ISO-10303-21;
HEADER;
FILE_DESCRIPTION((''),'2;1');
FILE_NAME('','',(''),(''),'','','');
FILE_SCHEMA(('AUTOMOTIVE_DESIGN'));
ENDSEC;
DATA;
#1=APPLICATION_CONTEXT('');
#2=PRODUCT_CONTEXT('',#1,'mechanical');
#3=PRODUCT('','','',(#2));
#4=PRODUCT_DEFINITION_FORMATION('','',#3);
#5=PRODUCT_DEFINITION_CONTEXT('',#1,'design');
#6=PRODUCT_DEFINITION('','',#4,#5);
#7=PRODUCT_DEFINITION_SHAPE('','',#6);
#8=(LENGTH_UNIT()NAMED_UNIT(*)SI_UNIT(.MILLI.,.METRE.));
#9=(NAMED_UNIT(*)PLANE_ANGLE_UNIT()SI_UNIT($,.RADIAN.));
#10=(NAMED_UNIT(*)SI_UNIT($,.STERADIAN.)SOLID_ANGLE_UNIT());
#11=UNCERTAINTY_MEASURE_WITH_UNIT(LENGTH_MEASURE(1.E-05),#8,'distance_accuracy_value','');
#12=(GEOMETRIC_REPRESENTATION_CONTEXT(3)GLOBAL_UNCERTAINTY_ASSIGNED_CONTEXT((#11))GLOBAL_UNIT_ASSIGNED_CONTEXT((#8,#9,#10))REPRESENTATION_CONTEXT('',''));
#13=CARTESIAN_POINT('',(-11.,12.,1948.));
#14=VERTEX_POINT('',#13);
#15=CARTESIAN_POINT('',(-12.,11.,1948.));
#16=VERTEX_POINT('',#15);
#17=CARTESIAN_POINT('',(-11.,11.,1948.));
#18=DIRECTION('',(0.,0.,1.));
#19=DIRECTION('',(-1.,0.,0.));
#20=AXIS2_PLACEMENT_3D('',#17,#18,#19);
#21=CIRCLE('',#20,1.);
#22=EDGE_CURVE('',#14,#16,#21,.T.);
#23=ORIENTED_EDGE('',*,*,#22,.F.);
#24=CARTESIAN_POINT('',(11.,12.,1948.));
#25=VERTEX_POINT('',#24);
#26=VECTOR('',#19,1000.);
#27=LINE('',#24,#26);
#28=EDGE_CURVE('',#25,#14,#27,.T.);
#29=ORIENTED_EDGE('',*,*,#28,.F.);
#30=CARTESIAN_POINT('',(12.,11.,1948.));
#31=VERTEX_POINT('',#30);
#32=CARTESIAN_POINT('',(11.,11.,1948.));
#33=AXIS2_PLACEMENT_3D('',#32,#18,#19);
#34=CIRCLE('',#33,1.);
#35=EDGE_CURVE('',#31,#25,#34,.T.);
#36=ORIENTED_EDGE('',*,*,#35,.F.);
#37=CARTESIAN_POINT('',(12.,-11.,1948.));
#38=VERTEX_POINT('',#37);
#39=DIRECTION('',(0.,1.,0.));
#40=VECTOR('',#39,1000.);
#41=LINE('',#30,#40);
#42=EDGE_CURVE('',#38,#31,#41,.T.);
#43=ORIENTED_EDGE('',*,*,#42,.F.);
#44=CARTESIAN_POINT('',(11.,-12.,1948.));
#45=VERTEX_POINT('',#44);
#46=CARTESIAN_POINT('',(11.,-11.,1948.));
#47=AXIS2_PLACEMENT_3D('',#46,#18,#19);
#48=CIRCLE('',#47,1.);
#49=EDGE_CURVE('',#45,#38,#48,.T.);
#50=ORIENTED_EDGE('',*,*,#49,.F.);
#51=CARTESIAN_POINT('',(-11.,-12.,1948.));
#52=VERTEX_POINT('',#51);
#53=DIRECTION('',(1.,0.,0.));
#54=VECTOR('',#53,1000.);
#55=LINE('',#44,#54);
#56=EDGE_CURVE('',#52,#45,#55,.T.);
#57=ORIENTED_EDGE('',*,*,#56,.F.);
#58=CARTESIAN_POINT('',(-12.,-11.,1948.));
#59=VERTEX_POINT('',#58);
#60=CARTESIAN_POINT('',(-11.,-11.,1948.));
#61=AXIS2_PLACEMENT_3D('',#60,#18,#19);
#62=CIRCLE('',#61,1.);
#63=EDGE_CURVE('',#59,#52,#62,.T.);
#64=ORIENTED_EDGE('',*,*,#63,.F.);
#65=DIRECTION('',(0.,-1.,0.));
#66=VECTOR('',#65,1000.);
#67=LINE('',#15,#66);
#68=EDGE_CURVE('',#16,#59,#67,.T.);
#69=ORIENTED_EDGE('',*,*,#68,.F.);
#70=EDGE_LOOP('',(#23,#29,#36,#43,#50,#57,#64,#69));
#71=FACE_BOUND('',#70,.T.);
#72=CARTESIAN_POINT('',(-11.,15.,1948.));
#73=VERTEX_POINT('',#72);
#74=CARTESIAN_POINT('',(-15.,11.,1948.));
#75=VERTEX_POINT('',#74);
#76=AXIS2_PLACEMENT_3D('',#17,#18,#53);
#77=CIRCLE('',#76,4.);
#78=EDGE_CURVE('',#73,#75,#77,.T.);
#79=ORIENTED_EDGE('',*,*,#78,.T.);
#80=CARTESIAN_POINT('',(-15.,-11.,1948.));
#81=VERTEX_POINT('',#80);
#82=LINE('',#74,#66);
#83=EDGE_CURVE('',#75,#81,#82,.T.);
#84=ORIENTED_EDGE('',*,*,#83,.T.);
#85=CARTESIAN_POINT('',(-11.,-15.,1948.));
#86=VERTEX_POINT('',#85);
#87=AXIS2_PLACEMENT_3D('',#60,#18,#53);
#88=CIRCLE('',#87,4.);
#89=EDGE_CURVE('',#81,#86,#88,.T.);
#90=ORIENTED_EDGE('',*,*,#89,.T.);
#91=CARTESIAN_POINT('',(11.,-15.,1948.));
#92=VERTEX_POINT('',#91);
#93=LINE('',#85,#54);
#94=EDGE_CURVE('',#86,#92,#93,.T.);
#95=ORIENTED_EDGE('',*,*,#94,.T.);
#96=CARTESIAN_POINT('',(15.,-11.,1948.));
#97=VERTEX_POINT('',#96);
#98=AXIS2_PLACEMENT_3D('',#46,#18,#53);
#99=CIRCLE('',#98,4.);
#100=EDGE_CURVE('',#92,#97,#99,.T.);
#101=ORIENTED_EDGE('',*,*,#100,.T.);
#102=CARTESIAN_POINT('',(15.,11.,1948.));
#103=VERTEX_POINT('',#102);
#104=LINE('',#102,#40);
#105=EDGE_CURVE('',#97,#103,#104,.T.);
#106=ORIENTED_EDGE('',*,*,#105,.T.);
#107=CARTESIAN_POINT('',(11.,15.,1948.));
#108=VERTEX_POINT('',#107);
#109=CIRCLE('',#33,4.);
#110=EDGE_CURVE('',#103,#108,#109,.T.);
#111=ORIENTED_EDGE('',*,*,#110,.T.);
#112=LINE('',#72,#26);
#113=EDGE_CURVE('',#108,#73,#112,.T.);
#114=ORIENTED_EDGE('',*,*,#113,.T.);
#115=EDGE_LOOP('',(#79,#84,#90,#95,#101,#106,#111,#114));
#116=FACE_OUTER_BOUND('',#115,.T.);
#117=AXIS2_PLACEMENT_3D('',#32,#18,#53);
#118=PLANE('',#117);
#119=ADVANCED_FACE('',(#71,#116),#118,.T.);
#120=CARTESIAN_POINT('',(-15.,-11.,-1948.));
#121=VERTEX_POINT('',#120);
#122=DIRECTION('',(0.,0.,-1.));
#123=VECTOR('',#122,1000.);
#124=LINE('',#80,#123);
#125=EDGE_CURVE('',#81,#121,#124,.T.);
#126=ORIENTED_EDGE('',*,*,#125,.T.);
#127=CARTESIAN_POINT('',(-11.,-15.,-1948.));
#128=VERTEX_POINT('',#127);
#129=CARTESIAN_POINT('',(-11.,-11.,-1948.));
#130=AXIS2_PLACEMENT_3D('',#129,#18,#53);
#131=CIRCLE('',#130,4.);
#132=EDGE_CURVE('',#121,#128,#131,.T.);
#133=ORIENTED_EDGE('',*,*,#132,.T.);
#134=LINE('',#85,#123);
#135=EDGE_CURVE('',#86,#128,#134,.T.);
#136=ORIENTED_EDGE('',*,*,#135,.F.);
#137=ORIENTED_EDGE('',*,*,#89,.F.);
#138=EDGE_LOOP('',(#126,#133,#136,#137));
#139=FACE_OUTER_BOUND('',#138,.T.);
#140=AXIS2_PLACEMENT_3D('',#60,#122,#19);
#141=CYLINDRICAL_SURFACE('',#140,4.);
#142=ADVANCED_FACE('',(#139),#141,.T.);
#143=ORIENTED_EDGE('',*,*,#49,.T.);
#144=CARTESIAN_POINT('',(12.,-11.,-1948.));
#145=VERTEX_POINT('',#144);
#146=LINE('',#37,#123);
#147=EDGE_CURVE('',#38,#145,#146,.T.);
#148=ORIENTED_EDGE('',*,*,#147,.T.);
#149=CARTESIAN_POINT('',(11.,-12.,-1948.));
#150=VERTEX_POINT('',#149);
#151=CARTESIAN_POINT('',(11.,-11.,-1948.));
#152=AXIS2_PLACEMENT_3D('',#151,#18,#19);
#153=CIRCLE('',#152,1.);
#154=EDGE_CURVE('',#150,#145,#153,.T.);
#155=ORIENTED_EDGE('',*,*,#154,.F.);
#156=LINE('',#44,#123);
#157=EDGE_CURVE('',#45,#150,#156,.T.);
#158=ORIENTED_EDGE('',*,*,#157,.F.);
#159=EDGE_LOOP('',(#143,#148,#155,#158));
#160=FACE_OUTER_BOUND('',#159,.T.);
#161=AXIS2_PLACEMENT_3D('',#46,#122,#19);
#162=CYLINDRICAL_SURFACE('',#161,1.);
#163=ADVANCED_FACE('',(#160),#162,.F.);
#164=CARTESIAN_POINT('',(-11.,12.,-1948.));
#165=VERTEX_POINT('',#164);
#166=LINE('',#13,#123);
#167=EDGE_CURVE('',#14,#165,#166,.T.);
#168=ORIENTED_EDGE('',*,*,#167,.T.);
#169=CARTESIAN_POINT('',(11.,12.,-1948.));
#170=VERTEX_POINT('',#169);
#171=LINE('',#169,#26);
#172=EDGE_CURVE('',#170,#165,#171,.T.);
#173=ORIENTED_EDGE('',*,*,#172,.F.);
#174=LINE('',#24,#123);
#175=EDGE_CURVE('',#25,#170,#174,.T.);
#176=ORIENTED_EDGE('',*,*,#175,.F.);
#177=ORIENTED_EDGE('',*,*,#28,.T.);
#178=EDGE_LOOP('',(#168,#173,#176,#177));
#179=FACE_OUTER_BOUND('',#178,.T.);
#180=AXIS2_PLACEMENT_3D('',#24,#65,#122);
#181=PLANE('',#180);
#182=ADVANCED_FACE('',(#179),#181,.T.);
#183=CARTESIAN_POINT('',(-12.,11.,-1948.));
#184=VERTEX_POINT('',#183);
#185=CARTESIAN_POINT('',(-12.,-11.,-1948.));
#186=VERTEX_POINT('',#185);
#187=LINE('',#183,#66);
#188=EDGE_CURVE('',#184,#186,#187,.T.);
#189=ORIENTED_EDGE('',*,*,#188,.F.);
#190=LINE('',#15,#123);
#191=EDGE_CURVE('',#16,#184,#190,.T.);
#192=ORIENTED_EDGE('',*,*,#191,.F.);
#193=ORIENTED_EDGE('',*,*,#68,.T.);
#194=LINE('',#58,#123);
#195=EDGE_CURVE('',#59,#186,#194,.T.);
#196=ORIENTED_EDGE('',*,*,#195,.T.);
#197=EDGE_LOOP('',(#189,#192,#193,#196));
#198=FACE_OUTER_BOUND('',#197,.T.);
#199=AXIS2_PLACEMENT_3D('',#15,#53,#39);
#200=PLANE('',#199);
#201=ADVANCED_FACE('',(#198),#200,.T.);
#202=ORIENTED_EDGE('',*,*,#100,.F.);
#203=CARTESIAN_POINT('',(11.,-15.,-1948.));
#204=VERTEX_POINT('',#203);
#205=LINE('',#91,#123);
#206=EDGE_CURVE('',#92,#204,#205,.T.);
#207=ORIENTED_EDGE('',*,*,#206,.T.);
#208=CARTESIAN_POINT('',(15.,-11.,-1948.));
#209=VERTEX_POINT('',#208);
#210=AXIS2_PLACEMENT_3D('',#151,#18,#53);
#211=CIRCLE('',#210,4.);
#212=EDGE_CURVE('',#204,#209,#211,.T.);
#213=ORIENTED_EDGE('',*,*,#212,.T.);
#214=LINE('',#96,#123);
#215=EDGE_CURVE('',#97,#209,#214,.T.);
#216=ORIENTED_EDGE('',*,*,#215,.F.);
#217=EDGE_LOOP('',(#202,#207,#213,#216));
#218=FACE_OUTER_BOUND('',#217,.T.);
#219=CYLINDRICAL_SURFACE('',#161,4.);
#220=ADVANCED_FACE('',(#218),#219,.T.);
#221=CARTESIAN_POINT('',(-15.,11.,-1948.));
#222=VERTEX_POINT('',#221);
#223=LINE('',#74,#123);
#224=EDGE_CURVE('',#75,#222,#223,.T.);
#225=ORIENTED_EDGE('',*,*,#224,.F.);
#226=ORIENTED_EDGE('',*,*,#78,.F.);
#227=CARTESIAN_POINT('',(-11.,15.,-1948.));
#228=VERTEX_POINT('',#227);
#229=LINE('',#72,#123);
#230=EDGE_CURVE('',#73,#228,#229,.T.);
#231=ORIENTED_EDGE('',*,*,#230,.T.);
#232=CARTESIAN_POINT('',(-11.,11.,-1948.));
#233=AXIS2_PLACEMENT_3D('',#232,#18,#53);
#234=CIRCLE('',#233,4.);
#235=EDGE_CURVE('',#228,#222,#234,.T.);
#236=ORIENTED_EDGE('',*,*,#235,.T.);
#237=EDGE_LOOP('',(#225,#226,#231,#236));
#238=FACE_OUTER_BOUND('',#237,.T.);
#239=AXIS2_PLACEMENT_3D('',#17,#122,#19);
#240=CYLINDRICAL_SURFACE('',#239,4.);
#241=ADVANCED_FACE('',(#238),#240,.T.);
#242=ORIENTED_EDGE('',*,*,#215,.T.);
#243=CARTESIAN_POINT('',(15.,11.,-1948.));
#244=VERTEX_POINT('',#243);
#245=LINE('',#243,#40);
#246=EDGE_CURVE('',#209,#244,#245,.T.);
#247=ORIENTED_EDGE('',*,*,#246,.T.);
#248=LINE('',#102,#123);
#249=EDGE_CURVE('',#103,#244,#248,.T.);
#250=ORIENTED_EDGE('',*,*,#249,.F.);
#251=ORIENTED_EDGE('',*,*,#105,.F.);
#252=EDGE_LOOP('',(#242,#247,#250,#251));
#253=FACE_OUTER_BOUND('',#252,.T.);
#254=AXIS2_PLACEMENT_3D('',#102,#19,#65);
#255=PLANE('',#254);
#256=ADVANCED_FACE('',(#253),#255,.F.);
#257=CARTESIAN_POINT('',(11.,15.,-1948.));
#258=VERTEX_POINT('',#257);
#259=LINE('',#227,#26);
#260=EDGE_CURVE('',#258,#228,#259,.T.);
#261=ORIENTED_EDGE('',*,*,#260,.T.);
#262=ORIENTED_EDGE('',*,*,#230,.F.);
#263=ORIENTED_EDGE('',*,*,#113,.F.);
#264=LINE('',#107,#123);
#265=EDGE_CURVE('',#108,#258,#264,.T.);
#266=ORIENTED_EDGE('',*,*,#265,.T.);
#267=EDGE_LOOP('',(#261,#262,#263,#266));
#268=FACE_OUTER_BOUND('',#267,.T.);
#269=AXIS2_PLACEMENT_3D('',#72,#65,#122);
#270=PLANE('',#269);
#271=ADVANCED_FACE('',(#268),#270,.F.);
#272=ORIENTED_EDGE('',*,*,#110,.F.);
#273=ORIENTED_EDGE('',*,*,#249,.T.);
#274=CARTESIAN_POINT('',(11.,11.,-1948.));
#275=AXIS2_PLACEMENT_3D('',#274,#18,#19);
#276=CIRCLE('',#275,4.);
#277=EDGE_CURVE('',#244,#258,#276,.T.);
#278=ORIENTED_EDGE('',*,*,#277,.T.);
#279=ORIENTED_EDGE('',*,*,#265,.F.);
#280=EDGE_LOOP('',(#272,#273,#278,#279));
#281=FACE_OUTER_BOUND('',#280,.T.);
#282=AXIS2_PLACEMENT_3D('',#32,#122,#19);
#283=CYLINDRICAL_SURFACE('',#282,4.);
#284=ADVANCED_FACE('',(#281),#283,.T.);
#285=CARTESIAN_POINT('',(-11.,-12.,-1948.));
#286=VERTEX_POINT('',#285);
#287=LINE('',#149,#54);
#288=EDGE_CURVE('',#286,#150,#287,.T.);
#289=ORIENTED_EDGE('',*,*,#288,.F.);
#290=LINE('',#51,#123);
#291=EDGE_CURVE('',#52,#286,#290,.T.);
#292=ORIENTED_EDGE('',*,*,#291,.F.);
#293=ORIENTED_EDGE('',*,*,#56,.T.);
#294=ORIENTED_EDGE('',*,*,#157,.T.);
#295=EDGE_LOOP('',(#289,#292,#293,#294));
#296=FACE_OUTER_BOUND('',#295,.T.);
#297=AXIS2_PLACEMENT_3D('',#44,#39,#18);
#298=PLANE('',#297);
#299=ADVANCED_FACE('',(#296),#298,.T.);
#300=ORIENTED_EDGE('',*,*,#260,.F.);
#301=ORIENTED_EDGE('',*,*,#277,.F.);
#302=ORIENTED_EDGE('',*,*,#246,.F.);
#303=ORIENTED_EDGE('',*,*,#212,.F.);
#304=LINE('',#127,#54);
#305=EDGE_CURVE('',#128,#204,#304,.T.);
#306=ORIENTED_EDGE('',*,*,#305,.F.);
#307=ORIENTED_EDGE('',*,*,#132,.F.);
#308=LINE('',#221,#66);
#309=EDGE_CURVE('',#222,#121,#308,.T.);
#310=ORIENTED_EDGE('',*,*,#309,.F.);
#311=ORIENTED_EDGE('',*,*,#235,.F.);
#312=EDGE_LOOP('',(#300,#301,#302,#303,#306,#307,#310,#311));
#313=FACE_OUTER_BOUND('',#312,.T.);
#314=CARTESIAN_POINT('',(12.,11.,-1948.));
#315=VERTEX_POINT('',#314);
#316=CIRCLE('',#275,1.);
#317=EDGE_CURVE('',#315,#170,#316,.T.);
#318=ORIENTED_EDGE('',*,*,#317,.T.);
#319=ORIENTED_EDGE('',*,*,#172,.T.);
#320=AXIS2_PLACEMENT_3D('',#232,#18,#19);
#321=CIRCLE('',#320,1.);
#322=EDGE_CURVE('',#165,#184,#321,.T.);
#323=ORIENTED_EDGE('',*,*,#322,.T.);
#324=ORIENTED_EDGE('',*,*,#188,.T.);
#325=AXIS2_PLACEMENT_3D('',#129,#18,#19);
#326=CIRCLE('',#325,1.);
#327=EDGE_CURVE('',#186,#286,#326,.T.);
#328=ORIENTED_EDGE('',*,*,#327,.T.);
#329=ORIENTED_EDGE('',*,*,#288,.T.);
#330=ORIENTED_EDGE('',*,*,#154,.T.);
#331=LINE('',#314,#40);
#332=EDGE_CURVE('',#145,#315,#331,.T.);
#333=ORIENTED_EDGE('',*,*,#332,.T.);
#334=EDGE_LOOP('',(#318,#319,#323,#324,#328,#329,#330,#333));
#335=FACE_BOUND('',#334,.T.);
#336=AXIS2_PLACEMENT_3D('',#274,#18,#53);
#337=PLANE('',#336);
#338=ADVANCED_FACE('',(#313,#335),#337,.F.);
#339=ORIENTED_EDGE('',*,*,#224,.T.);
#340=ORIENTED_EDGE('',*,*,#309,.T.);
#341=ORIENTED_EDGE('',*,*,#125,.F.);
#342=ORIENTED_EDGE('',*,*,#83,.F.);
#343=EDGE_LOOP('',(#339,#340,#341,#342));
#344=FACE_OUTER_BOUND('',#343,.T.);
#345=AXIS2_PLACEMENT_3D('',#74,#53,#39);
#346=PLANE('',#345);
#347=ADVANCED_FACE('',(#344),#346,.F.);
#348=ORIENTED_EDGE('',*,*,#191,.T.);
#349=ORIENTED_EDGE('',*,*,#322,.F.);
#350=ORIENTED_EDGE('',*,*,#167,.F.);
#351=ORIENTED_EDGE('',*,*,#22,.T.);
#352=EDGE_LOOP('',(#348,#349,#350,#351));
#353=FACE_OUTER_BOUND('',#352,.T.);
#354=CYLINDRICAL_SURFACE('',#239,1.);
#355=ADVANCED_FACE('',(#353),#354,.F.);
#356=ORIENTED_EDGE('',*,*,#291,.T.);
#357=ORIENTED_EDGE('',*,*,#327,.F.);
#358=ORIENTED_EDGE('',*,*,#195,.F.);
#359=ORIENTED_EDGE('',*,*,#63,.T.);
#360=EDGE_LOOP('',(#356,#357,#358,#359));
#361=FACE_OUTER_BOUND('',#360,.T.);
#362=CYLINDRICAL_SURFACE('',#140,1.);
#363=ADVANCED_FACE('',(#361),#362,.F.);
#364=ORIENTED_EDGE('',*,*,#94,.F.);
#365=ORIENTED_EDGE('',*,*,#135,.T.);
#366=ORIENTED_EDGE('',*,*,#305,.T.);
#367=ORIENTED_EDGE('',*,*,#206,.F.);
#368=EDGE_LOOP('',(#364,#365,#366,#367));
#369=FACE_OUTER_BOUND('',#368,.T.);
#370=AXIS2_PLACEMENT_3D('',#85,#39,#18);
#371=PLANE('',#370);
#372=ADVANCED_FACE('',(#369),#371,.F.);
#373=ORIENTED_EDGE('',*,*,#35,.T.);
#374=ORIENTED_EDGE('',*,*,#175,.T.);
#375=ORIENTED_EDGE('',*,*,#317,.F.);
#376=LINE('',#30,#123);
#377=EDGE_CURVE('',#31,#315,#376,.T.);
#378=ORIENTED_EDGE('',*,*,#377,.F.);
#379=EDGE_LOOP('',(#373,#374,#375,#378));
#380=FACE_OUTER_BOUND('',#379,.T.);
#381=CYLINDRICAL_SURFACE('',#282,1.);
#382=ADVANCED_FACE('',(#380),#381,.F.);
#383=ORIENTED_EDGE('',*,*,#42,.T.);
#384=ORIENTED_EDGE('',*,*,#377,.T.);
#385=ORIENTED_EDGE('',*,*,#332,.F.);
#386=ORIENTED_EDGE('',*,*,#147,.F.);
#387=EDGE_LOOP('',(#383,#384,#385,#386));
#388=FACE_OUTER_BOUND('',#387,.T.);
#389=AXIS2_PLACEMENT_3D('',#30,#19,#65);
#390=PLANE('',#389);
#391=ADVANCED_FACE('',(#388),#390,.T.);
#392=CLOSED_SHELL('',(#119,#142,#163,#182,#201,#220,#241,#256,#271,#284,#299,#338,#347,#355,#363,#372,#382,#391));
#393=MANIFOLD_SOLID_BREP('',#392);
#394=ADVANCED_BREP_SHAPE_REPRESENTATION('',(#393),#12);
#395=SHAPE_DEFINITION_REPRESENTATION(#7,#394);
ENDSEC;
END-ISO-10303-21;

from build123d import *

# Parameters (mm, degrees)
EXTRUDE_1_DEPTH = 1948


with BuildPart() as part:
    # 草图2 → 拉伸-薄壁1 (new, symmetric)
    with BuildSketch(Plane.XY):
        with BuildLine():
            Line((-11, 15), (11, 15))
            ThreePointArc((11, 15), (13.828427125, 13.828427125), (15, 11))
            Line((15, 11), (15, -11))
            ThreePointArc((15, -11), (13.828427125, -13.828427125), (11, -15))
            Line((11, -15), (-11, -15))
            ThreePointArc((-11, -15), (-13.828427125, -13.828427125), (-15, -11))
            Line((-15, -11), (-15, 11))
            ThreePointArc((-15, 11), (-13.828427125, 13.828427125), (-11, 15))
        make_face()
        with BuildLine():
            Line((-11, 12), (11, 12))
            ThreePointArc((11, 12), (11.707106781, 11.707106781), (12, 11))
            Line((12, 11), (12, -11))
            ThreePointArc((12, -11), (11.707106781, -11.707106781), (11, -12))
            Line((11, -12), (-11, -12))
            ThreePointArc((-11, -12), (-11.707106781, -11.707106781), (-12, -11))
            Line((-12, -11), (-12, 11))
            ThreePointArc((-12, 11), (-11.707106781, 11.707106781), (-11, 12))
        make_face(mode=Mode.SUBTRACT)
    extrude(amount=EXTRUDE_1_DEPTH, both=True)


solid = part.part
